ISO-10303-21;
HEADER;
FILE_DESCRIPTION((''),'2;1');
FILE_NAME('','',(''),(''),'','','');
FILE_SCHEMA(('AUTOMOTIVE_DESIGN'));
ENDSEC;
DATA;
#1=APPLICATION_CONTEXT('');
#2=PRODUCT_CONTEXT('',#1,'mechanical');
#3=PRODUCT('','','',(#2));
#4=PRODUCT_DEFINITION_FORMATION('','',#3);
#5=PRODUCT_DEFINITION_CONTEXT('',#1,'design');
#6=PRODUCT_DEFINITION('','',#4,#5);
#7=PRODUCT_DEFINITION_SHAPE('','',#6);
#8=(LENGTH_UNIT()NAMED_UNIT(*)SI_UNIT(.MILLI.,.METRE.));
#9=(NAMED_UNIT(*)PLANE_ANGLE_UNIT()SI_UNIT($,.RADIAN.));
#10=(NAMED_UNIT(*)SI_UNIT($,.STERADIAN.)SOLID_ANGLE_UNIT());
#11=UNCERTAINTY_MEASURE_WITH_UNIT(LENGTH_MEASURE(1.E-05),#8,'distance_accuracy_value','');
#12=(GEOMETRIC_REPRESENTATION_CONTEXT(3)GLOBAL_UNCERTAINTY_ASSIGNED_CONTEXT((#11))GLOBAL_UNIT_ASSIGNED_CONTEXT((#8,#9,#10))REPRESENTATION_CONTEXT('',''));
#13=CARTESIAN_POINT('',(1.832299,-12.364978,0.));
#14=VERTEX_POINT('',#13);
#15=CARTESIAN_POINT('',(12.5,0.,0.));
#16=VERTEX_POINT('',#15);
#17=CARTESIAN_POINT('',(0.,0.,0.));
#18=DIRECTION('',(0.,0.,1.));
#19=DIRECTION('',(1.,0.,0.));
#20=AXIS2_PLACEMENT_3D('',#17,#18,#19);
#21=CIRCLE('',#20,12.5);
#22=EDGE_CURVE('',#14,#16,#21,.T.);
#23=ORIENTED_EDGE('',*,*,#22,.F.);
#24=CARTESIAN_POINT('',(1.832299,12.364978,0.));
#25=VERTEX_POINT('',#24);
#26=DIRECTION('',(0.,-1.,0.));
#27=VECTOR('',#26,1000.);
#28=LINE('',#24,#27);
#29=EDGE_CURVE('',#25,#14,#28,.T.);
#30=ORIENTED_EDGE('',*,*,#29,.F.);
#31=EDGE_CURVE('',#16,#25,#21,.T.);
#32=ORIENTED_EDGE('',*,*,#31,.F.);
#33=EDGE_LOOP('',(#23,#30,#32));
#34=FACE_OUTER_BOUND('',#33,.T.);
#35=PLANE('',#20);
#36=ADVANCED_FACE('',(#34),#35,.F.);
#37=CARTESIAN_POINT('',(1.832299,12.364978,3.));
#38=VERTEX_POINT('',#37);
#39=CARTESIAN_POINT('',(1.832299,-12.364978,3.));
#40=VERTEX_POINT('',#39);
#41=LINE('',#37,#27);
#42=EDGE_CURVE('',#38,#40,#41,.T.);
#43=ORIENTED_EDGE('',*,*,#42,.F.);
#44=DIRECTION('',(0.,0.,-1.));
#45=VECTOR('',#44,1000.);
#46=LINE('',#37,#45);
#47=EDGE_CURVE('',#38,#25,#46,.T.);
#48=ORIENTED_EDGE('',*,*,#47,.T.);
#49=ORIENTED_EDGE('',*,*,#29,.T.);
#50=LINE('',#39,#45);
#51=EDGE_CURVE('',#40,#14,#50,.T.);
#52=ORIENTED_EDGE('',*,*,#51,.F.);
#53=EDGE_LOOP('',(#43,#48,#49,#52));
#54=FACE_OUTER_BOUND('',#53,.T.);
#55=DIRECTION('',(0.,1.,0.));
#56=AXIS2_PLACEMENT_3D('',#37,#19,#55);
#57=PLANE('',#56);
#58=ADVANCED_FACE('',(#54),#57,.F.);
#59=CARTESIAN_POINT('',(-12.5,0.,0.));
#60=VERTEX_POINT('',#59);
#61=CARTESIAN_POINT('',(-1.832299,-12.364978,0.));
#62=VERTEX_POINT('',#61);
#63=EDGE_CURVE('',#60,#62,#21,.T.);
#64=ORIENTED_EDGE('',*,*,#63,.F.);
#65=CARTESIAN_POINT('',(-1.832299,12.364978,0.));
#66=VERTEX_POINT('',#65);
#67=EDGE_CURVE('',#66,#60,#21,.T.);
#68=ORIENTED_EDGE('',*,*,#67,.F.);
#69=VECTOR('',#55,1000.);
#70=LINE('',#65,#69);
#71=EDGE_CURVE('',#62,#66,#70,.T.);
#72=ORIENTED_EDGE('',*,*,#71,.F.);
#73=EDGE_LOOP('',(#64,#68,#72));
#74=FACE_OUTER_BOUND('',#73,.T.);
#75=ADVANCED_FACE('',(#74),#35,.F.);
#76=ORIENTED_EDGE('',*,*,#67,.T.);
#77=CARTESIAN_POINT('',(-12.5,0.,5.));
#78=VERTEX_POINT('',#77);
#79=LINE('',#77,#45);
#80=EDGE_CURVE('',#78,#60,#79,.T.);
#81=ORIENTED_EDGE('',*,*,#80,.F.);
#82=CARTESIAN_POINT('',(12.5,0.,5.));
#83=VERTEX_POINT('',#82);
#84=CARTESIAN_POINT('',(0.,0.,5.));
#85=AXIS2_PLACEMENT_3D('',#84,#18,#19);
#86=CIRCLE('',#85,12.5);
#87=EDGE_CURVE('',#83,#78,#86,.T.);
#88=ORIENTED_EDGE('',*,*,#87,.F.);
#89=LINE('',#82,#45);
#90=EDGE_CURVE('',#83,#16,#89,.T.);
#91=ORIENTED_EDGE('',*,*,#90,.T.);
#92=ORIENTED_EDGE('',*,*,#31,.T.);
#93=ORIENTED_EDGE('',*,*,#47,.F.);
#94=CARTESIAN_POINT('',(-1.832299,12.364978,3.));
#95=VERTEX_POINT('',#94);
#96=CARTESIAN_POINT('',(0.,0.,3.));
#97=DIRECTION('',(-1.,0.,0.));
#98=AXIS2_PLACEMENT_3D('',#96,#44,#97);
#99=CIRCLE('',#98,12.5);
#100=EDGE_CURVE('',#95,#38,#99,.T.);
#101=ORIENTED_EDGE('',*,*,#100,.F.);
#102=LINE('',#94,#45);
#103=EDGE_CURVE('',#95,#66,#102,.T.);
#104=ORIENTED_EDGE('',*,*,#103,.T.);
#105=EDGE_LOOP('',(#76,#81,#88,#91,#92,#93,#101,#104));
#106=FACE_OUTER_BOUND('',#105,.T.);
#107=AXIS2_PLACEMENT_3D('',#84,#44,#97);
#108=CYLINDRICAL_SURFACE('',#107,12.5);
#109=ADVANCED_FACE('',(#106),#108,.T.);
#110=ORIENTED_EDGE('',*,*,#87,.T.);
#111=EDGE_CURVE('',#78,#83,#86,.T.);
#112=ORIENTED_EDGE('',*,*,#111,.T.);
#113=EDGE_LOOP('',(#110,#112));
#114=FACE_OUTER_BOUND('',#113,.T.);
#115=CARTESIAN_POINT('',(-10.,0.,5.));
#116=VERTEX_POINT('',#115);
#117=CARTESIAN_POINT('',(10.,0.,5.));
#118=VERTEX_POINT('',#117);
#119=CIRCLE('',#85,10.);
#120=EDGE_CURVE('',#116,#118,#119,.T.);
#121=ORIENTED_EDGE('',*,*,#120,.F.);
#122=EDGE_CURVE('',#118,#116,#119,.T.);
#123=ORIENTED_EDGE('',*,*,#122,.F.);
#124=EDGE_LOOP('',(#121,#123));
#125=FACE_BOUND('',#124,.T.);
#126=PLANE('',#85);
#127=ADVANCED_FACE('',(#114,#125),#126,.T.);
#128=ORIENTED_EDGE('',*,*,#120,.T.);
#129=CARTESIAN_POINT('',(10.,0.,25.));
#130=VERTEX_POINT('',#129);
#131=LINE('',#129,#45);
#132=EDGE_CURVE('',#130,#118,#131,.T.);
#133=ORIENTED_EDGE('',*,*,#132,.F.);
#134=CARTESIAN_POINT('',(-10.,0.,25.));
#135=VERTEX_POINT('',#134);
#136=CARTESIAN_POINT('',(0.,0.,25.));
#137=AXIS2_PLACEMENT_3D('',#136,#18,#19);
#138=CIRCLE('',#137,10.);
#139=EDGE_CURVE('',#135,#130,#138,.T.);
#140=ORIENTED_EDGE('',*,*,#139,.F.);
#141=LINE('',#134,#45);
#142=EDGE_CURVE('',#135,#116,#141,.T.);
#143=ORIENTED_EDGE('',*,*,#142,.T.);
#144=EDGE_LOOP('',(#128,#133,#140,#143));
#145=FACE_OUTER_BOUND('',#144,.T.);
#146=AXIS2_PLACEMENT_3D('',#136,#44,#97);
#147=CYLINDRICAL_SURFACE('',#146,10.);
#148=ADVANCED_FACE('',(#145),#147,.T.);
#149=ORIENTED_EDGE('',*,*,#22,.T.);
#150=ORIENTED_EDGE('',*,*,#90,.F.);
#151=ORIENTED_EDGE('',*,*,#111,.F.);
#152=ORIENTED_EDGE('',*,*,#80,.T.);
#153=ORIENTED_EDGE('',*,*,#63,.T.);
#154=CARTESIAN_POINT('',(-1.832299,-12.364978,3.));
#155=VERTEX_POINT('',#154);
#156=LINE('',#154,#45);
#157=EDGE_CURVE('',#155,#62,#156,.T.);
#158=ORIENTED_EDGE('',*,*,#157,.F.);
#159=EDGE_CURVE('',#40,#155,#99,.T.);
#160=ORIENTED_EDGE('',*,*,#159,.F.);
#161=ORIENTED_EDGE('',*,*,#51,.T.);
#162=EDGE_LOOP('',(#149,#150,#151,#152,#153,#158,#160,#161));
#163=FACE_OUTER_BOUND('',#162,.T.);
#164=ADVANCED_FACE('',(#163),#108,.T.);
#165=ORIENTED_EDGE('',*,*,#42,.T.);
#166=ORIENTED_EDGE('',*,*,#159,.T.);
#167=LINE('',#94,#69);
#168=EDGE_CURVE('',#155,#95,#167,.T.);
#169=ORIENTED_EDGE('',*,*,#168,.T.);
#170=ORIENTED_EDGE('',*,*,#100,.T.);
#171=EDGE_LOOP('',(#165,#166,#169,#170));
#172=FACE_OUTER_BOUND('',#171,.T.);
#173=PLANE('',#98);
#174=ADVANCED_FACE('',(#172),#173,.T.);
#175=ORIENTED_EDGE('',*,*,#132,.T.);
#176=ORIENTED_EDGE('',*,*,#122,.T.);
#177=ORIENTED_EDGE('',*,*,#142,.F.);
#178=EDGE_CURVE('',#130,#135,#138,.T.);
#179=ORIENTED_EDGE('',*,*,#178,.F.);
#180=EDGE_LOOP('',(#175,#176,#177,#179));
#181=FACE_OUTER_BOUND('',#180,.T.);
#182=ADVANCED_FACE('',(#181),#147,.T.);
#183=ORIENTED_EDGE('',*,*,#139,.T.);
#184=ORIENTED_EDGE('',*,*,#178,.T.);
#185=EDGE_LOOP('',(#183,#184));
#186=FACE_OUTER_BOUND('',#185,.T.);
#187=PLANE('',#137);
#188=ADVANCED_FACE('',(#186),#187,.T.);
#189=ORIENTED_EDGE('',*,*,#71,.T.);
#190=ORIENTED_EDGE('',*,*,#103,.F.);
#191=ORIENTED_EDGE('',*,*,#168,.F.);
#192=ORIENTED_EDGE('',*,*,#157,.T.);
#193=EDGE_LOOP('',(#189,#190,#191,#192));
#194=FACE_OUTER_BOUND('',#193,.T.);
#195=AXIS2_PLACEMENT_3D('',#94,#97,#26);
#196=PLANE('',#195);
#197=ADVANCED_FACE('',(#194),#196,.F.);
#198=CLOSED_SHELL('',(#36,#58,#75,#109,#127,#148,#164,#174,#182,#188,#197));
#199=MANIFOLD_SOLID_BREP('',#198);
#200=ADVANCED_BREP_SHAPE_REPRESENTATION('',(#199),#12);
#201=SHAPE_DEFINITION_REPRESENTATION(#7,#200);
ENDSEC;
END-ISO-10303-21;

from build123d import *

# Parameters (mm, degrees)
SKETCH1_R           = 12.5
BOSS_EXTRUDE1_DEPTH = 5
SKETCH2_R           = 10
BOSS_EXTRUDE2_DEPTH = 20
CUT_EXTRUDE2_DEPTH  = 3


with BuildPart() as part:
    # Sketch1 → Boss-Extrude1 (new body)
    with BuildSketch(Plane.XY):
        Circle(SKETCH1_R)
    extrude(amount=BOSS_EXTRUDE1_DEPTH)

    # Sketch2 → Boss-Extrude2 (add)
    with BuildSketch(Plane.XY.offset(5)):
        Circle(SKETCH2_R)
    extrude(amount=BOSS_EXTRUDE2_DEPTH)

    # Sketch3 → Cut-Extrude2 (cut)
    with BuildSketch(Plane(origin=(0, 0, 0), x_dir=(-1, 0, 0), z_dir=(0, 0, -1))):
        with BuildLine():
            Line((1.83229916, 12.364977953), (1.83229916, -12.364977953))
            ThreePointArc((1.83229916, -12.364977953), (0, -12.5), (-1.83229916, -12.364977953))
            Line((-1.83229916, -12.364977953), (-1.83229916, 12.364977953))
            ThreePointArc((-1.83229916, 12.364977953), (0, 12.5), (1.83229916, 12.364977953))
        make_face()
    extrude(amount=-CUT_EXTRUDE2_DEPTH, mode=Mode.SUBTRACT)


solid = part.part
